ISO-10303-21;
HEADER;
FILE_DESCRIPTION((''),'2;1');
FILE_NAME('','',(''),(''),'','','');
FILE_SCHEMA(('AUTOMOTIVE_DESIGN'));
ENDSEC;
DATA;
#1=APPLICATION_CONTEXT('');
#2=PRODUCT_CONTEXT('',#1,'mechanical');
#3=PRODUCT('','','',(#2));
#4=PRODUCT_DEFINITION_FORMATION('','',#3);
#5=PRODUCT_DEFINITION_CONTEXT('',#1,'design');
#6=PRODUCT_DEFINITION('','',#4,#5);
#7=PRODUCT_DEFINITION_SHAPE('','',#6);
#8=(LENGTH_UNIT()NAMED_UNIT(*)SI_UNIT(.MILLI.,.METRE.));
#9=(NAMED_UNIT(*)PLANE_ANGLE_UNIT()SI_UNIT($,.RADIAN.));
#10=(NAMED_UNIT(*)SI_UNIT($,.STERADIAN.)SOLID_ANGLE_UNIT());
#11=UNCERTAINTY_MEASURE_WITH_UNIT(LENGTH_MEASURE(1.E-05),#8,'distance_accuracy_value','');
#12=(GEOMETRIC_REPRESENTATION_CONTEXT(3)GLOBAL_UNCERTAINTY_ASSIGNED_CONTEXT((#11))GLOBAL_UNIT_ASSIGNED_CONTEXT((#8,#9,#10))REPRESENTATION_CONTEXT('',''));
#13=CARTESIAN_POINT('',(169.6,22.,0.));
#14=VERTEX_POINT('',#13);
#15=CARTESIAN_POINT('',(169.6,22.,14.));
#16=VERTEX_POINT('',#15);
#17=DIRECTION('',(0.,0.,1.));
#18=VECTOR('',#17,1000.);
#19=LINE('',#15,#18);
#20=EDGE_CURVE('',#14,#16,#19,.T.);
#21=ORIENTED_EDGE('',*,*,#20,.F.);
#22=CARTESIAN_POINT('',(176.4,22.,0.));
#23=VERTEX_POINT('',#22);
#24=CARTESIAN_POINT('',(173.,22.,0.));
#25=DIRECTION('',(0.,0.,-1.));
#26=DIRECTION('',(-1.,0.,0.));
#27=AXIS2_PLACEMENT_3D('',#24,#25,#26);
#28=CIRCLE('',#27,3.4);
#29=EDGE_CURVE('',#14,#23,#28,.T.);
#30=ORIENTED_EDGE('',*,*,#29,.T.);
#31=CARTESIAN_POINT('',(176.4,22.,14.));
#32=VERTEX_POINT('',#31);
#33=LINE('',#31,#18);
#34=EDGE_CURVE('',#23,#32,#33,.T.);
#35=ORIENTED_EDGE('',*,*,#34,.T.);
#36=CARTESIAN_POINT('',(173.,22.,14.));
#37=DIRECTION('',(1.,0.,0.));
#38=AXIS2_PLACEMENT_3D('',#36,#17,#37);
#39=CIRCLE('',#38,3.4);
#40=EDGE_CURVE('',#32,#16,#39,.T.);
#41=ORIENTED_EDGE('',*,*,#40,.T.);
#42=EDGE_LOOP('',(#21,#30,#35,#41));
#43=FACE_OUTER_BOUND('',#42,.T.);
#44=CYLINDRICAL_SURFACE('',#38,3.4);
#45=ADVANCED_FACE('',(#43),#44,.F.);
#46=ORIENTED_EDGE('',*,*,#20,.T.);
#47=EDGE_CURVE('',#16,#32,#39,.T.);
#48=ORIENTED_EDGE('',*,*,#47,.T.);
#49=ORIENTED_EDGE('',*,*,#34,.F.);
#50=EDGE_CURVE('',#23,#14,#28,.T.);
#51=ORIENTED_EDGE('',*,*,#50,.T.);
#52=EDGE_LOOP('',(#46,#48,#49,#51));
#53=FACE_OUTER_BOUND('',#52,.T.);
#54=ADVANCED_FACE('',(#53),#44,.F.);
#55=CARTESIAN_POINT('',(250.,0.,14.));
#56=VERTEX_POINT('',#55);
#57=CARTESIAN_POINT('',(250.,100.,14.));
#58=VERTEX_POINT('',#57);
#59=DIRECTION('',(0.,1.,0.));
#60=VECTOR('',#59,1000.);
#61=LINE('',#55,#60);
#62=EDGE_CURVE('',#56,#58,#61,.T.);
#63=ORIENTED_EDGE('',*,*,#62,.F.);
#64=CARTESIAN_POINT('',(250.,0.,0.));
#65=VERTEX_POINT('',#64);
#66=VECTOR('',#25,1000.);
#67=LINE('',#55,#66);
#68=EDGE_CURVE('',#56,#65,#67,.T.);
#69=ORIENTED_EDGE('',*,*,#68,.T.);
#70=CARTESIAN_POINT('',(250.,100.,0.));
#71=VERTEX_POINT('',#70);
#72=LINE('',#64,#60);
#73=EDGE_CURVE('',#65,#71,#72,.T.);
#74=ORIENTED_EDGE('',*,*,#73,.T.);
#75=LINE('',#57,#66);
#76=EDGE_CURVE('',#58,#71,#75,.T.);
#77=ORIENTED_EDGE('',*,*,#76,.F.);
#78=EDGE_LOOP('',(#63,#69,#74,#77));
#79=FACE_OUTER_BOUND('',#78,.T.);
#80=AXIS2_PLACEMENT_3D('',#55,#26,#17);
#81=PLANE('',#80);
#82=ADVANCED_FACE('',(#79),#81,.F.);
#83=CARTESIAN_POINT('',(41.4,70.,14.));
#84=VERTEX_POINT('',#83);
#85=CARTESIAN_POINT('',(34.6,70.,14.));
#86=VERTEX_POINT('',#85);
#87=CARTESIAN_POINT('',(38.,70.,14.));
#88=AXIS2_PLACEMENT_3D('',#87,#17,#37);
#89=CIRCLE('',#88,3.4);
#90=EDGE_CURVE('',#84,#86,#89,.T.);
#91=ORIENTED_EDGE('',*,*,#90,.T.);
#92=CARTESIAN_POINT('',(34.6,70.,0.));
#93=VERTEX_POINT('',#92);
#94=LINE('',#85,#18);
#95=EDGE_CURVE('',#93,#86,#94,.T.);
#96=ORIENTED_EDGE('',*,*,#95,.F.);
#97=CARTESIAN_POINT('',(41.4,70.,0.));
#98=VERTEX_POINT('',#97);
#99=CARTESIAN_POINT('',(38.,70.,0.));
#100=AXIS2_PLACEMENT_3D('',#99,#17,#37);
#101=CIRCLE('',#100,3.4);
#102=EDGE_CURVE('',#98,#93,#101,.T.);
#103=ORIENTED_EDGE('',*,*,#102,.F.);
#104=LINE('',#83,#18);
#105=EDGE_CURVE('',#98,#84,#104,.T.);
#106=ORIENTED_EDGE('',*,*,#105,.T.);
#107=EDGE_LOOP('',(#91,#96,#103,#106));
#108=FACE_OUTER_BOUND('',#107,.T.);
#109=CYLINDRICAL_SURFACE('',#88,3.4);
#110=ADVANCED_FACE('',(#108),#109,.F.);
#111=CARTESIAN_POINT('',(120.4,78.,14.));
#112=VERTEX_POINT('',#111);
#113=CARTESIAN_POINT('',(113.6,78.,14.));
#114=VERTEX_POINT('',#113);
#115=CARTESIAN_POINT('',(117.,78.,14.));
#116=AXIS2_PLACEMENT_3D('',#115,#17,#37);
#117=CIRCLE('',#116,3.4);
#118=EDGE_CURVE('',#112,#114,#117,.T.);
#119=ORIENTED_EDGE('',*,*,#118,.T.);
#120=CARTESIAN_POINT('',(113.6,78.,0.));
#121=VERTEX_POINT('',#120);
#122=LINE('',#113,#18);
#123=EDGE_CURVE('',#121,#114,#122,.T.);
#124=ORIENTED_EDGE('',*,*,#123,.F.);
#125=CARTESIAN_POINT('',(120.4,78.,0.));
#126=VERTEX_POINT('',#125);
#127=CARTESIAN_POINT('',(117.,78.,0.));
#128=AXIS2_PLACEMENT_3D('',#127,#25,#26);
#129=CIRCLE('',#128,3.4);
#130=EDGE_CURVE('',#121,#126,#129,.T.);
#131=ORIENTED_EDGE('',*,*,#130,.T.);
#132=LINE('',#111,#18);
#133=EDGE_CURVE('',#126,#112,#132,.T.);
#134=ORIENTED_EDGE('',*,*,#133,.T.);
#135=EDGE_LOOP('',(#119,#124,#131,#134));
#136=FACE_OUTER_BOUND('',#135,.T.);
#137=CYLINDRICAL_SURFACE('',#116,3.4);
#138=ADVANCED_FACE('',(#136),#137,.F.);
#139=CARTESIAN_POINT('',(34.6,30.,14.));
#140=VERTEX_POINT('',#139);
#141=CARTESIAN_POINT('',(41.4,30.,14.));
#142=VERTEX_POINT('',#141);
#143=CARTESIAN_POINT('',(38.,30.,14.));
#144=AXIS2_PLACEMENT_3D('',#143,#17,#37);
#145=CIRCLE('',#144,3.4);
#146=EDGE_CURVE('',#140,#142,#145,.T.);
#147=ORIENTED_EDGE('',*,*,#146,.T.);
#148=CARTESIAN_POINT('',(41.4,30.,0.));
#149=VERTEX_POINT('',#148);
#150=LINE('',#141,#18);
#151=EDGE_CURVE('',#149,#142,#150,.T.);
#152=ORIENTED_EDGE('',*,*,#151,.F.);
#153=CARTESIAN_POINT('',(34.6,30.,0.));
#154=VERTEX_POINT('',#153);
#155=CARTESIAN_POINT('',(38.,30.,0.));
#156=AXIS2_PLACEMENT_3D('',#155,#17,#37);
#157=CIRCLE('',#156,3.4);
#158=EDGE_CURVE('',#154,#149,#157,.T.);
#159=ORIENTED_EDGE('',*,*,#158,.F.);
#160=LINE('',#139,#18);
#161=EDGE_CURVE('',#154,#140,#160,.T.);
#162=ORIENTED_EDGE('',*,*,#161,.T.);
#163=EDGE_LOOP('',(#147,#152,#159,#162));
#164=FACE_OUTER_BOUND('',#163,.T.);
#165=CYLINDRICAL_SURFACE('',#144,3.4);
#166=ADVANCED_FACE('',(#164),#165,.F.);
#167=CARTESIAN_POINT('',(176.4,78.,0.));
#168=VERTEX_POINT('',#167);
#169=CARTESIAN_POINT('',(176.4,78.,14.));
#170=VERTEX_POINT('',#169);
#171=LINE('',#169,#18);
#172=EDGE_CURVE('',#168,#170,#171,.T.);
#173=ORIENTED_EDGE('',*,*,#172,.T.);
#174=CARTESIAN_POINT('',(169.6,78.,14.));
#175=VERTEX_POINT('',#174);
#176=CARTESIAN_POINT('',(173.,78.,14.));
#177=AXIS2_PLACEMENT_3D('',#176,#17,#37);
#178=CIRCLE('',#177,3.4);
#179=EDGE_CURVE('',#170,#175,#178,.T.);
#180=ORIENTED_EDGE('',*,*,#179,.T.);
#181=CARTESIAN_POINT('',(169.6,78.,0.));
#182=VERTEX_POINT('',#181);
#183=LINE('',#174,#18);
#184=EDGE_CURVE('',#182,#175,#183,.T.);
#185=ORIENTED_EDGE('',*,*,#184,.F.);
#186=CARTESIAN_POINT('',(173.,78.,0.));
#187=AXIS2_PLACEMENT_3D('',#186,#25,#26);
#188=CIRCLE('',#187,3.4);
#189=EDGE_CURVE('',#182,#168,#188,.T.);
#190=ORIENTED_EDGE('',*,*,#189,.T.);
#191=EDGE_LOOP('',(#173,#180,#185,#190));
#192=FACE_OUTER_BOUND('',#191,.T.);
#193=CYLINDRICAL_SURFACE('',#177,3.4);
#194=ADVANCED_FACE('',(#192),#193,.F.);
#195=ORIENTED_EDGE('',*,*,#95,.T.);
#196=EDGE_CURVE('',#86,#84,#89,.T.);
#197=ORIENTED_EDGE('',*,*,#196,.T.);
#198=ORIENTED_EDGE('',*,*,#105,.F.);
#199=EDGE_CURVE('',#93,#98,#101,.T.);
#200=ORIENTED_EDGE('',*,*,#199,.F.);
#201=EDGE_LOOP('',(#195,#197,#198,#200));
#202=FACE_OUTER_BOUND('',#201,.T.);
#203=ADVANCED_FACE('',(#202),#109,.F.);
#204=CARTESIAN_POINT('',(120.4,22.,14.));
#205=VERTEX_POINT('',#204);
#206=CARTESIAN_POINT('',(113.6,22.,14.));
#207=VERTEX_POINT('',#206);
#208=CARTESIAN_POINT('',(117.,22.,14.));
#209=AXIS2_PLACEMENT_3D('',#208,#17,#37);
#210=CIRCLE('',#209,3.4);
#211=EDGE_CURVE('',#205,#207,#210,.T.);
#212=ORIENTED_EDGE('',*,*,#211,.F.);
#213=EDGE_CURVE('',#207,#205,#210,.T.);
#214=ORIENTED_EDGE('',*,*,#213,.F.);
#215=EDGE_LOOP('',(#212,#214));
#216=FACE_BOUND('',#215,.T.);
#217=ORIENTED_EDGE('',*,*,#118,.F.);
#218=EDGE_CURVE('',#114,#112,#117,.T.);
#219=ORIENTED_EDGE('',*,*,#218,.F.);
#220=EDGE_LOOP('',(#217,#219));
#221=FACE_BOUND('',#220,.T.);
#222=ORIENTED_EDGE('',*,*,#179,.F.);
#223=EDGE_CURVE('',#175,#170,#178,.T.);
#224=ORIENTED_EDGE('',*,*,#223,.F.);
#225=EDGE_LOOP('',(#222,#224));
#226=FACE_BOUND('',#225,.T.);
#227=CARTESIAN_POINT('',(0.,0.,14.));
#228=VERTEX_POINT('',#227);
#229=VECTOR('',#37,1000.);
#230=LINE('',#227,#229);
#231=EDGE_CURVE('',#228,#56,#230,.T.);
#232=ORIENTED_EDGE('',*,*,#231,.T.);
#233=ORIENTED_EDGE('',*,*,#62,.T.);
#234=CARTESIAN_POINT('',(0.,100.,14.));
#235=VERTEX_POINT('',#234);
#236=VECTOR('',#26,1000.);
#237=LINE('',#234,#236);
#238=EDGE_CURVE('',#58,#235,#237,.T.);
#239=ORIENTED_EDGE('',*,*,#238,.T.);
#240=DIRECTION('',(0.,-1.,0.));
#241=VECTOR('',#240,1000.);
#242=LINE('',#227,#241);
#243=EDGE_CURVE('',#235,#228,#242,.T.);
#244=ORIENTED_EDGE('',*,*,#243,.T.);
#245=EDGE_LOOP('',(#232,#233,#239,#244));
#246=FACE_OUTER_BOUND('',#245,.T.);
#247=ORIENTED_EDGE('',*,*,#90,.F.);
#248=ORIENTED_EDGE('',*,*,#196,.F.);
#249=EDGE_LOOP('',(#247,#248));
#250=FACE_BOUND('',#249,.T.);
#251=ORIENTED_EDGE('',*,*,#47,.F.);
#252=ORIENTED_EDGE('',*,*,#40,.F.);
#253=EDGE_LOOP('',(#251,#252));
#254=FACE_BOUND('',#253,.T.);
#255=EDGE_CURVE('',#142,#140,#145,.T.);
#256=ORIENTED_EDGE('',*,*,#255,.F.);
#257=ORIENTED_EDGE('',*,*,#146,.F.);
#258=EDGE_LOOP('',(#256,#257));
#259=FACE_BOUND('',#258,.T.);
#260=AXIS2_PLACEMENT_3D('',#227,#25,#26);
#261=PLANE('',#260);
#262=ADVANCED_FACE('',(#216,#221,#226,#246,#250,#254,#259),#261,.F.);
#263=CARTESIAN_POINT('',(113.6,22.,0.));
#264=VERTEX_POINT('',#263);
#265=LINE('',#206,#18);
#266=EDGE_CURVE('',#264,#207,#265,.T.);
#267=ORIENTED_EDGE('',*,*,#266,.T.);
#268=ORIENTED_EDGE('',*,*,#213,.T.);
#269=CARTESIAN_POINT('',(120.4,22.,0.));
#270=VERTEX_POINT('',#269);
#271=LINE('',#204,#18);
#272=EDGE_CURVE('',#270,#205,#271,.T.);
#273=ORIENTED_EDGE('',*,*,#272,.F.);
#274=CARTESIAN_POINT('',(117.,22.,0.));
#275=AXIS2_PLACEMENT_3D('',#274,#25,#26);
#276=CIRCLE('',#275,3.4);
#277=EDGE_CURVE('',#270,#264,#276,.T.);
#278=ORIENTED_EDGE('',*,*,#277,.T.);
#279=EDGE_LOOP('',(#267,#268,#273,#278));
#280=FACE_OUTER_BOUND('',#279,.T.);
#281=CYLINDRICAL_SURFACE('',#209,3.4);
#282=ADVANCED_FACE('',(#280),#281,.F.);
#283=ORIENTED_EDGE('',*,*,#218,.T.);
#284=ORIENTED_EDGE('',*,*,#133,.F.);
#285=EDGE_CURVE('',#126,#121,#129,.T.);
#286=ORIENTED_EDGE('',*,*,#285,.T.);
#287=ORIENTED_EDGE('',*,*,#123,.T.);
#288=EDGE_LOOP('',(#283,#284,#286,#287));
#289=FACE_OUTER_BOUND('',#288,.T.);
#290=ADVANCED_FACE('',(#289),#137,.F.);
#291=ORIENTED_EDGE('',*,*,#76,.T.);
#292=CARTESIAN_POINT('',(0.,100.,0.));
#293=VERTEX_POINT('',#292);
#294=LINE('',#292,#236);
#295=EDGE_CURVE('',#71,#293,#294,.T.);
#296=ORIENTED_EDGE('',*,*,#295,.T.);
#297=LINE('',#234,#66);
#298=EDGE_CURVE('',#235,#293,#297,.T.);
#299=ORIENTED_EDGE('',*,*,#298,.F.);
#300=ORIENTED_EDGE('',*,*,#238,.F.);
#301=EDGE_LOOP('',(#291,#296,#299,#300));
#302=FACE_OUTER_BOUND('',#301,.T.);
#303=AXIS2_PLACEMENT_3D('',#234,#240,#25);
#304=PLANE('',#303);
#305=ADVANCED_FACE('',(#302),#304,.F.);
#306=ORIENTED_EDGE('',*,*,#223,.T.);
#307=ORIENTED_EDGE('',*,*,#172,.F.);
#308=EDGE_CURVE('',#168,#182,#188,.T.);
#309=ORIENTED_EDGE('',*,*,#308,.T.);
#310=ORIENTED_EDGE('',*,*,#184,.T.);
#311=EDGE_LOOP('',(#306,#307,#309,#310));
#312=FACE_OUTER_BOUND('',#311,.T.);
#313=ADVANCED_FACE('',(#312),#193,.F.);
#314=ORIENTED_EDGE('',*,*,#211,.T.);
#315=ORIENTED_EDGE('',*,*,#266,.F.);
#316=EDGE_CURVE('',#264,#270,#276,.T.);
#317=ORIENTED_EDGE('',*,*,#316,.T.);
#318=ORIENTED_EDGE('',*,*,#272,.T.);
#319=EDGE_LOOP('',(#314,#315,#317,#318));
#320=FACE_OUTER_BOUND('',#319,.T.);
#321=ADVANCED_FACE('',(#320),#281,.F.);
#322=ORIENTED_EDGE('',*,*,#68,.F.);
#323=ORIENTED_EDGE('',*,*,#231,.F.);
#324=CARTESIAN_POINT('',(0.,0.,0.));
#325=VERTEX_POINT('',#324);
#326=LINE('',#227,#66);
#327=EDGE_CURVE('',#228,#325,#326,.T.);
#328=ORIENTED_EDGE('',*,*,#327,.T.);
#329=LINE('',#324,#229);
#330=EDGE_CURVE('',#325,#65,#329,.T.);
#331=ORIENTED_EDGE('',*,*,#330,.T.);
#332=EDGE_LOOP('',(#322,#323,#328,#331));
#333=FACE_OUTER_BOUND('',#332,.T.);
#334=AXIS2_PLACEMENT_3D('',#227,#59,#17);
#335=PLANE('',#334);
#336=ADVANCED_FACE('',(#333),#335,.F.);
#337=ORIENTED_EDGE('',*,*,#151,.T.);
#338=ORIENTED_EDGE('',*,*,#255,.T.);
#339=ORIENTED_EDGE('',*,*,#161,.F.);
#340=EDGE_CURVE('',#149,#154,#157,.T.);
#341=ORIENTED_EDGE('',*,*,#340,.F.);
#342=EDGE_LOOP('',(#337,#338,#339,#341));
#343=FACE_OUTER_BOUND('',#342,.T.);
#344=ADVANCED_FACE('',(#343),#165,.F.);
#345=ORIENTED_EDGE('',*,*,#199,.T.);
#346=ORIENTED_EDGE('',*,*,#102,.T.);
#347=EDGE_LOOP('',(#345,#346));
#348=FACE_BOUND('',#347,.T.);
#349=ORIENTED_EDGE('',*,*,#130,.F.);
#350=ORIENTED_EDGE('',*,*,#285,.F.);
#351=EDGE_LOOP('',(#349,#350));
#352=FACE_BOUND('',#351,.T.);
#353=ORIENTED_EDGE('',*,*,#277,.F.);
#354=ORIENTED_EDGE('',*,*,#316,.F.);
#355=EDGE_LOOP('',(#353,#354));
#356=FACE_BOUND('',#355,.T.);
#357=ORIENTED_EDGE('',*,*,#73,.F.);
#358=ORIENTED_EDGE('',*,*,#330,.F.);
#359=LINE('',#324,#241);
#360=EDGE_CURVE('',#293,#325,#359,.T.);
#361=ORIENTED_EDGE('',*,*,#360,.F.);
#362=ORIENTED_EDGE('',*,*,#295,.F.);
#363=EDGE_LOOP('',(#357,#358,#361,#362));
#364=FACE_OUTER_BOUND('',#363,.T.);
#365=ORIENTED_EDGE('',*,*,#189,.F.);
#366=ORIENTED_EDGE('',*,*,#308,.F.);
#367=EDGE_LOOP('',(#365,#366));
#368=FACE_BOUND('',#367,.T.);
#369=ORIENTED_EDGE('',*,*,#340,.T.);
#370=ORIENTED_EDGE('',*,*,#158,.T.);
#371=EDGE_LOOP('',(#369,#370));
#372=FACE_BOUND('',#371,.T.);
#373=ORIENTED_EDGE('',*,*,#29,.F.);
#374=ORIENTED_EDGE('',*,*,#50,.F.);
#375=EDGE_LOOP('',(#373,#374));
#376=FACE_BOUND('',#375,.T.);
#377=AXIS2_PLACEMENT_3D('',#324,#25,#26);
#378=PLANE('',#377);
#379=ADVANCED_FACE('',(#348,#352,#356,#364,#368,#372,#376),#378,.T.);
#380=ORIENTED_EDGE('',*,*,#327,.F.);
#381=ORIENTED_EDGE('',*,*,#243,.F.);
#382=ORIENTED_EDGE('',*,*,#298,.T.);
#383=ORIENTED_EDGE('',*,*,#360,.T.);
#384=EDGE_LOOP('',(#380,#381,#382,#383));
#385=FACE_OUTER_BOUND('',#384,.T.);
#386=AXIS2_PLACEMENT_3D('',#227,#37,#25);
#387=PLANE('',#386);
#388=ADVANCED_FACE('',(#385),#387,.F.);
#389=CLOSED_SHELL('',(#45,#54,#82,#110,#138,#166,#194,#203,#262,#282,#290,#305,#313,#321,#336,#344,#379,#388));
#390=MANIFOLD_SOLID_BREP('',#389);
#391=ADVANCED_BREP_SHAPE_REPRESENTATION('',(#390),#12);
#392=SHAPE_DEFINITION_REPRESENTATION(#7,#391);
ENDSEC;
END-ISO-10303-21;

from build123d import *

# Parameters (mm, degrees)
SKETCH1_W             = 250
SKETCH1_H             = 100
SKETCH1_R             = 2.5
BOSS_EXTRUDE1_DEPTH   = 14
M8_TAPPED_HOLE1_D     = 6.8
M8_TAPPED_HOLE1_DEPTH = 19.75
M8_TAPPED_HOLE1_TIP   = 2.042926105
M8_TAPPED_HOLE2_D     = 6.8


with BuildPart() as part:
    # Sketch1 → Boss-Extrude1 (new body)
    with BuildSketch(Plane.XY):
        with Locations((125, 50)):
            Rectangle(SKETCH1_W, SKETCH1_H)
        with Locations((117, 78)):
            Circle(SKETCH1_R, mode=Mode.SUBTRACT)
        with Locations((173, 78)):
            Circle(SKETCH1_R, mode=Mode.SUBTRACT)
        with Locations((117, 22)):
            Circle(SKETCH1_R, mode=Mode.SUBTRACT)
        with Locations((173, 22)):
            Circle(SKETCH1_R, mode=Mode.SUBTRACT)
    extrude(amount=BOSS_EXTRUDE1_DEPTH)

    # M8 Tapped Hole1
    with Locations(Plane.XY.offset(14)):
        with Locations((117, 78), (173, 78), (117, 22), (173, 22)):
            Hole(M8_TAPPED_HOLE1_D / 2, depth=M8_TAPPED_HOLE1_DEPTH)
            with Locations((0, 0, -(M8_TAPPED_HOLE1_DEPTH + M8_TAPPED_HOLE1_TIP / 2))):  # 118° drill point
                Cone(0, M8_TAPPED_HOLE1_D / 2, M8_TAPPED_HOLE1_TIP, mode=Mode.SUBTRACT)

    # M8 Tapped Hole2 (through all)
    with Locations(Plane.XY.offset(14)):
        with Locations((38, 70), (38, 30)):
            Hole(M8_TAPPED_HOLE2_D / 2)


solid = part.part
